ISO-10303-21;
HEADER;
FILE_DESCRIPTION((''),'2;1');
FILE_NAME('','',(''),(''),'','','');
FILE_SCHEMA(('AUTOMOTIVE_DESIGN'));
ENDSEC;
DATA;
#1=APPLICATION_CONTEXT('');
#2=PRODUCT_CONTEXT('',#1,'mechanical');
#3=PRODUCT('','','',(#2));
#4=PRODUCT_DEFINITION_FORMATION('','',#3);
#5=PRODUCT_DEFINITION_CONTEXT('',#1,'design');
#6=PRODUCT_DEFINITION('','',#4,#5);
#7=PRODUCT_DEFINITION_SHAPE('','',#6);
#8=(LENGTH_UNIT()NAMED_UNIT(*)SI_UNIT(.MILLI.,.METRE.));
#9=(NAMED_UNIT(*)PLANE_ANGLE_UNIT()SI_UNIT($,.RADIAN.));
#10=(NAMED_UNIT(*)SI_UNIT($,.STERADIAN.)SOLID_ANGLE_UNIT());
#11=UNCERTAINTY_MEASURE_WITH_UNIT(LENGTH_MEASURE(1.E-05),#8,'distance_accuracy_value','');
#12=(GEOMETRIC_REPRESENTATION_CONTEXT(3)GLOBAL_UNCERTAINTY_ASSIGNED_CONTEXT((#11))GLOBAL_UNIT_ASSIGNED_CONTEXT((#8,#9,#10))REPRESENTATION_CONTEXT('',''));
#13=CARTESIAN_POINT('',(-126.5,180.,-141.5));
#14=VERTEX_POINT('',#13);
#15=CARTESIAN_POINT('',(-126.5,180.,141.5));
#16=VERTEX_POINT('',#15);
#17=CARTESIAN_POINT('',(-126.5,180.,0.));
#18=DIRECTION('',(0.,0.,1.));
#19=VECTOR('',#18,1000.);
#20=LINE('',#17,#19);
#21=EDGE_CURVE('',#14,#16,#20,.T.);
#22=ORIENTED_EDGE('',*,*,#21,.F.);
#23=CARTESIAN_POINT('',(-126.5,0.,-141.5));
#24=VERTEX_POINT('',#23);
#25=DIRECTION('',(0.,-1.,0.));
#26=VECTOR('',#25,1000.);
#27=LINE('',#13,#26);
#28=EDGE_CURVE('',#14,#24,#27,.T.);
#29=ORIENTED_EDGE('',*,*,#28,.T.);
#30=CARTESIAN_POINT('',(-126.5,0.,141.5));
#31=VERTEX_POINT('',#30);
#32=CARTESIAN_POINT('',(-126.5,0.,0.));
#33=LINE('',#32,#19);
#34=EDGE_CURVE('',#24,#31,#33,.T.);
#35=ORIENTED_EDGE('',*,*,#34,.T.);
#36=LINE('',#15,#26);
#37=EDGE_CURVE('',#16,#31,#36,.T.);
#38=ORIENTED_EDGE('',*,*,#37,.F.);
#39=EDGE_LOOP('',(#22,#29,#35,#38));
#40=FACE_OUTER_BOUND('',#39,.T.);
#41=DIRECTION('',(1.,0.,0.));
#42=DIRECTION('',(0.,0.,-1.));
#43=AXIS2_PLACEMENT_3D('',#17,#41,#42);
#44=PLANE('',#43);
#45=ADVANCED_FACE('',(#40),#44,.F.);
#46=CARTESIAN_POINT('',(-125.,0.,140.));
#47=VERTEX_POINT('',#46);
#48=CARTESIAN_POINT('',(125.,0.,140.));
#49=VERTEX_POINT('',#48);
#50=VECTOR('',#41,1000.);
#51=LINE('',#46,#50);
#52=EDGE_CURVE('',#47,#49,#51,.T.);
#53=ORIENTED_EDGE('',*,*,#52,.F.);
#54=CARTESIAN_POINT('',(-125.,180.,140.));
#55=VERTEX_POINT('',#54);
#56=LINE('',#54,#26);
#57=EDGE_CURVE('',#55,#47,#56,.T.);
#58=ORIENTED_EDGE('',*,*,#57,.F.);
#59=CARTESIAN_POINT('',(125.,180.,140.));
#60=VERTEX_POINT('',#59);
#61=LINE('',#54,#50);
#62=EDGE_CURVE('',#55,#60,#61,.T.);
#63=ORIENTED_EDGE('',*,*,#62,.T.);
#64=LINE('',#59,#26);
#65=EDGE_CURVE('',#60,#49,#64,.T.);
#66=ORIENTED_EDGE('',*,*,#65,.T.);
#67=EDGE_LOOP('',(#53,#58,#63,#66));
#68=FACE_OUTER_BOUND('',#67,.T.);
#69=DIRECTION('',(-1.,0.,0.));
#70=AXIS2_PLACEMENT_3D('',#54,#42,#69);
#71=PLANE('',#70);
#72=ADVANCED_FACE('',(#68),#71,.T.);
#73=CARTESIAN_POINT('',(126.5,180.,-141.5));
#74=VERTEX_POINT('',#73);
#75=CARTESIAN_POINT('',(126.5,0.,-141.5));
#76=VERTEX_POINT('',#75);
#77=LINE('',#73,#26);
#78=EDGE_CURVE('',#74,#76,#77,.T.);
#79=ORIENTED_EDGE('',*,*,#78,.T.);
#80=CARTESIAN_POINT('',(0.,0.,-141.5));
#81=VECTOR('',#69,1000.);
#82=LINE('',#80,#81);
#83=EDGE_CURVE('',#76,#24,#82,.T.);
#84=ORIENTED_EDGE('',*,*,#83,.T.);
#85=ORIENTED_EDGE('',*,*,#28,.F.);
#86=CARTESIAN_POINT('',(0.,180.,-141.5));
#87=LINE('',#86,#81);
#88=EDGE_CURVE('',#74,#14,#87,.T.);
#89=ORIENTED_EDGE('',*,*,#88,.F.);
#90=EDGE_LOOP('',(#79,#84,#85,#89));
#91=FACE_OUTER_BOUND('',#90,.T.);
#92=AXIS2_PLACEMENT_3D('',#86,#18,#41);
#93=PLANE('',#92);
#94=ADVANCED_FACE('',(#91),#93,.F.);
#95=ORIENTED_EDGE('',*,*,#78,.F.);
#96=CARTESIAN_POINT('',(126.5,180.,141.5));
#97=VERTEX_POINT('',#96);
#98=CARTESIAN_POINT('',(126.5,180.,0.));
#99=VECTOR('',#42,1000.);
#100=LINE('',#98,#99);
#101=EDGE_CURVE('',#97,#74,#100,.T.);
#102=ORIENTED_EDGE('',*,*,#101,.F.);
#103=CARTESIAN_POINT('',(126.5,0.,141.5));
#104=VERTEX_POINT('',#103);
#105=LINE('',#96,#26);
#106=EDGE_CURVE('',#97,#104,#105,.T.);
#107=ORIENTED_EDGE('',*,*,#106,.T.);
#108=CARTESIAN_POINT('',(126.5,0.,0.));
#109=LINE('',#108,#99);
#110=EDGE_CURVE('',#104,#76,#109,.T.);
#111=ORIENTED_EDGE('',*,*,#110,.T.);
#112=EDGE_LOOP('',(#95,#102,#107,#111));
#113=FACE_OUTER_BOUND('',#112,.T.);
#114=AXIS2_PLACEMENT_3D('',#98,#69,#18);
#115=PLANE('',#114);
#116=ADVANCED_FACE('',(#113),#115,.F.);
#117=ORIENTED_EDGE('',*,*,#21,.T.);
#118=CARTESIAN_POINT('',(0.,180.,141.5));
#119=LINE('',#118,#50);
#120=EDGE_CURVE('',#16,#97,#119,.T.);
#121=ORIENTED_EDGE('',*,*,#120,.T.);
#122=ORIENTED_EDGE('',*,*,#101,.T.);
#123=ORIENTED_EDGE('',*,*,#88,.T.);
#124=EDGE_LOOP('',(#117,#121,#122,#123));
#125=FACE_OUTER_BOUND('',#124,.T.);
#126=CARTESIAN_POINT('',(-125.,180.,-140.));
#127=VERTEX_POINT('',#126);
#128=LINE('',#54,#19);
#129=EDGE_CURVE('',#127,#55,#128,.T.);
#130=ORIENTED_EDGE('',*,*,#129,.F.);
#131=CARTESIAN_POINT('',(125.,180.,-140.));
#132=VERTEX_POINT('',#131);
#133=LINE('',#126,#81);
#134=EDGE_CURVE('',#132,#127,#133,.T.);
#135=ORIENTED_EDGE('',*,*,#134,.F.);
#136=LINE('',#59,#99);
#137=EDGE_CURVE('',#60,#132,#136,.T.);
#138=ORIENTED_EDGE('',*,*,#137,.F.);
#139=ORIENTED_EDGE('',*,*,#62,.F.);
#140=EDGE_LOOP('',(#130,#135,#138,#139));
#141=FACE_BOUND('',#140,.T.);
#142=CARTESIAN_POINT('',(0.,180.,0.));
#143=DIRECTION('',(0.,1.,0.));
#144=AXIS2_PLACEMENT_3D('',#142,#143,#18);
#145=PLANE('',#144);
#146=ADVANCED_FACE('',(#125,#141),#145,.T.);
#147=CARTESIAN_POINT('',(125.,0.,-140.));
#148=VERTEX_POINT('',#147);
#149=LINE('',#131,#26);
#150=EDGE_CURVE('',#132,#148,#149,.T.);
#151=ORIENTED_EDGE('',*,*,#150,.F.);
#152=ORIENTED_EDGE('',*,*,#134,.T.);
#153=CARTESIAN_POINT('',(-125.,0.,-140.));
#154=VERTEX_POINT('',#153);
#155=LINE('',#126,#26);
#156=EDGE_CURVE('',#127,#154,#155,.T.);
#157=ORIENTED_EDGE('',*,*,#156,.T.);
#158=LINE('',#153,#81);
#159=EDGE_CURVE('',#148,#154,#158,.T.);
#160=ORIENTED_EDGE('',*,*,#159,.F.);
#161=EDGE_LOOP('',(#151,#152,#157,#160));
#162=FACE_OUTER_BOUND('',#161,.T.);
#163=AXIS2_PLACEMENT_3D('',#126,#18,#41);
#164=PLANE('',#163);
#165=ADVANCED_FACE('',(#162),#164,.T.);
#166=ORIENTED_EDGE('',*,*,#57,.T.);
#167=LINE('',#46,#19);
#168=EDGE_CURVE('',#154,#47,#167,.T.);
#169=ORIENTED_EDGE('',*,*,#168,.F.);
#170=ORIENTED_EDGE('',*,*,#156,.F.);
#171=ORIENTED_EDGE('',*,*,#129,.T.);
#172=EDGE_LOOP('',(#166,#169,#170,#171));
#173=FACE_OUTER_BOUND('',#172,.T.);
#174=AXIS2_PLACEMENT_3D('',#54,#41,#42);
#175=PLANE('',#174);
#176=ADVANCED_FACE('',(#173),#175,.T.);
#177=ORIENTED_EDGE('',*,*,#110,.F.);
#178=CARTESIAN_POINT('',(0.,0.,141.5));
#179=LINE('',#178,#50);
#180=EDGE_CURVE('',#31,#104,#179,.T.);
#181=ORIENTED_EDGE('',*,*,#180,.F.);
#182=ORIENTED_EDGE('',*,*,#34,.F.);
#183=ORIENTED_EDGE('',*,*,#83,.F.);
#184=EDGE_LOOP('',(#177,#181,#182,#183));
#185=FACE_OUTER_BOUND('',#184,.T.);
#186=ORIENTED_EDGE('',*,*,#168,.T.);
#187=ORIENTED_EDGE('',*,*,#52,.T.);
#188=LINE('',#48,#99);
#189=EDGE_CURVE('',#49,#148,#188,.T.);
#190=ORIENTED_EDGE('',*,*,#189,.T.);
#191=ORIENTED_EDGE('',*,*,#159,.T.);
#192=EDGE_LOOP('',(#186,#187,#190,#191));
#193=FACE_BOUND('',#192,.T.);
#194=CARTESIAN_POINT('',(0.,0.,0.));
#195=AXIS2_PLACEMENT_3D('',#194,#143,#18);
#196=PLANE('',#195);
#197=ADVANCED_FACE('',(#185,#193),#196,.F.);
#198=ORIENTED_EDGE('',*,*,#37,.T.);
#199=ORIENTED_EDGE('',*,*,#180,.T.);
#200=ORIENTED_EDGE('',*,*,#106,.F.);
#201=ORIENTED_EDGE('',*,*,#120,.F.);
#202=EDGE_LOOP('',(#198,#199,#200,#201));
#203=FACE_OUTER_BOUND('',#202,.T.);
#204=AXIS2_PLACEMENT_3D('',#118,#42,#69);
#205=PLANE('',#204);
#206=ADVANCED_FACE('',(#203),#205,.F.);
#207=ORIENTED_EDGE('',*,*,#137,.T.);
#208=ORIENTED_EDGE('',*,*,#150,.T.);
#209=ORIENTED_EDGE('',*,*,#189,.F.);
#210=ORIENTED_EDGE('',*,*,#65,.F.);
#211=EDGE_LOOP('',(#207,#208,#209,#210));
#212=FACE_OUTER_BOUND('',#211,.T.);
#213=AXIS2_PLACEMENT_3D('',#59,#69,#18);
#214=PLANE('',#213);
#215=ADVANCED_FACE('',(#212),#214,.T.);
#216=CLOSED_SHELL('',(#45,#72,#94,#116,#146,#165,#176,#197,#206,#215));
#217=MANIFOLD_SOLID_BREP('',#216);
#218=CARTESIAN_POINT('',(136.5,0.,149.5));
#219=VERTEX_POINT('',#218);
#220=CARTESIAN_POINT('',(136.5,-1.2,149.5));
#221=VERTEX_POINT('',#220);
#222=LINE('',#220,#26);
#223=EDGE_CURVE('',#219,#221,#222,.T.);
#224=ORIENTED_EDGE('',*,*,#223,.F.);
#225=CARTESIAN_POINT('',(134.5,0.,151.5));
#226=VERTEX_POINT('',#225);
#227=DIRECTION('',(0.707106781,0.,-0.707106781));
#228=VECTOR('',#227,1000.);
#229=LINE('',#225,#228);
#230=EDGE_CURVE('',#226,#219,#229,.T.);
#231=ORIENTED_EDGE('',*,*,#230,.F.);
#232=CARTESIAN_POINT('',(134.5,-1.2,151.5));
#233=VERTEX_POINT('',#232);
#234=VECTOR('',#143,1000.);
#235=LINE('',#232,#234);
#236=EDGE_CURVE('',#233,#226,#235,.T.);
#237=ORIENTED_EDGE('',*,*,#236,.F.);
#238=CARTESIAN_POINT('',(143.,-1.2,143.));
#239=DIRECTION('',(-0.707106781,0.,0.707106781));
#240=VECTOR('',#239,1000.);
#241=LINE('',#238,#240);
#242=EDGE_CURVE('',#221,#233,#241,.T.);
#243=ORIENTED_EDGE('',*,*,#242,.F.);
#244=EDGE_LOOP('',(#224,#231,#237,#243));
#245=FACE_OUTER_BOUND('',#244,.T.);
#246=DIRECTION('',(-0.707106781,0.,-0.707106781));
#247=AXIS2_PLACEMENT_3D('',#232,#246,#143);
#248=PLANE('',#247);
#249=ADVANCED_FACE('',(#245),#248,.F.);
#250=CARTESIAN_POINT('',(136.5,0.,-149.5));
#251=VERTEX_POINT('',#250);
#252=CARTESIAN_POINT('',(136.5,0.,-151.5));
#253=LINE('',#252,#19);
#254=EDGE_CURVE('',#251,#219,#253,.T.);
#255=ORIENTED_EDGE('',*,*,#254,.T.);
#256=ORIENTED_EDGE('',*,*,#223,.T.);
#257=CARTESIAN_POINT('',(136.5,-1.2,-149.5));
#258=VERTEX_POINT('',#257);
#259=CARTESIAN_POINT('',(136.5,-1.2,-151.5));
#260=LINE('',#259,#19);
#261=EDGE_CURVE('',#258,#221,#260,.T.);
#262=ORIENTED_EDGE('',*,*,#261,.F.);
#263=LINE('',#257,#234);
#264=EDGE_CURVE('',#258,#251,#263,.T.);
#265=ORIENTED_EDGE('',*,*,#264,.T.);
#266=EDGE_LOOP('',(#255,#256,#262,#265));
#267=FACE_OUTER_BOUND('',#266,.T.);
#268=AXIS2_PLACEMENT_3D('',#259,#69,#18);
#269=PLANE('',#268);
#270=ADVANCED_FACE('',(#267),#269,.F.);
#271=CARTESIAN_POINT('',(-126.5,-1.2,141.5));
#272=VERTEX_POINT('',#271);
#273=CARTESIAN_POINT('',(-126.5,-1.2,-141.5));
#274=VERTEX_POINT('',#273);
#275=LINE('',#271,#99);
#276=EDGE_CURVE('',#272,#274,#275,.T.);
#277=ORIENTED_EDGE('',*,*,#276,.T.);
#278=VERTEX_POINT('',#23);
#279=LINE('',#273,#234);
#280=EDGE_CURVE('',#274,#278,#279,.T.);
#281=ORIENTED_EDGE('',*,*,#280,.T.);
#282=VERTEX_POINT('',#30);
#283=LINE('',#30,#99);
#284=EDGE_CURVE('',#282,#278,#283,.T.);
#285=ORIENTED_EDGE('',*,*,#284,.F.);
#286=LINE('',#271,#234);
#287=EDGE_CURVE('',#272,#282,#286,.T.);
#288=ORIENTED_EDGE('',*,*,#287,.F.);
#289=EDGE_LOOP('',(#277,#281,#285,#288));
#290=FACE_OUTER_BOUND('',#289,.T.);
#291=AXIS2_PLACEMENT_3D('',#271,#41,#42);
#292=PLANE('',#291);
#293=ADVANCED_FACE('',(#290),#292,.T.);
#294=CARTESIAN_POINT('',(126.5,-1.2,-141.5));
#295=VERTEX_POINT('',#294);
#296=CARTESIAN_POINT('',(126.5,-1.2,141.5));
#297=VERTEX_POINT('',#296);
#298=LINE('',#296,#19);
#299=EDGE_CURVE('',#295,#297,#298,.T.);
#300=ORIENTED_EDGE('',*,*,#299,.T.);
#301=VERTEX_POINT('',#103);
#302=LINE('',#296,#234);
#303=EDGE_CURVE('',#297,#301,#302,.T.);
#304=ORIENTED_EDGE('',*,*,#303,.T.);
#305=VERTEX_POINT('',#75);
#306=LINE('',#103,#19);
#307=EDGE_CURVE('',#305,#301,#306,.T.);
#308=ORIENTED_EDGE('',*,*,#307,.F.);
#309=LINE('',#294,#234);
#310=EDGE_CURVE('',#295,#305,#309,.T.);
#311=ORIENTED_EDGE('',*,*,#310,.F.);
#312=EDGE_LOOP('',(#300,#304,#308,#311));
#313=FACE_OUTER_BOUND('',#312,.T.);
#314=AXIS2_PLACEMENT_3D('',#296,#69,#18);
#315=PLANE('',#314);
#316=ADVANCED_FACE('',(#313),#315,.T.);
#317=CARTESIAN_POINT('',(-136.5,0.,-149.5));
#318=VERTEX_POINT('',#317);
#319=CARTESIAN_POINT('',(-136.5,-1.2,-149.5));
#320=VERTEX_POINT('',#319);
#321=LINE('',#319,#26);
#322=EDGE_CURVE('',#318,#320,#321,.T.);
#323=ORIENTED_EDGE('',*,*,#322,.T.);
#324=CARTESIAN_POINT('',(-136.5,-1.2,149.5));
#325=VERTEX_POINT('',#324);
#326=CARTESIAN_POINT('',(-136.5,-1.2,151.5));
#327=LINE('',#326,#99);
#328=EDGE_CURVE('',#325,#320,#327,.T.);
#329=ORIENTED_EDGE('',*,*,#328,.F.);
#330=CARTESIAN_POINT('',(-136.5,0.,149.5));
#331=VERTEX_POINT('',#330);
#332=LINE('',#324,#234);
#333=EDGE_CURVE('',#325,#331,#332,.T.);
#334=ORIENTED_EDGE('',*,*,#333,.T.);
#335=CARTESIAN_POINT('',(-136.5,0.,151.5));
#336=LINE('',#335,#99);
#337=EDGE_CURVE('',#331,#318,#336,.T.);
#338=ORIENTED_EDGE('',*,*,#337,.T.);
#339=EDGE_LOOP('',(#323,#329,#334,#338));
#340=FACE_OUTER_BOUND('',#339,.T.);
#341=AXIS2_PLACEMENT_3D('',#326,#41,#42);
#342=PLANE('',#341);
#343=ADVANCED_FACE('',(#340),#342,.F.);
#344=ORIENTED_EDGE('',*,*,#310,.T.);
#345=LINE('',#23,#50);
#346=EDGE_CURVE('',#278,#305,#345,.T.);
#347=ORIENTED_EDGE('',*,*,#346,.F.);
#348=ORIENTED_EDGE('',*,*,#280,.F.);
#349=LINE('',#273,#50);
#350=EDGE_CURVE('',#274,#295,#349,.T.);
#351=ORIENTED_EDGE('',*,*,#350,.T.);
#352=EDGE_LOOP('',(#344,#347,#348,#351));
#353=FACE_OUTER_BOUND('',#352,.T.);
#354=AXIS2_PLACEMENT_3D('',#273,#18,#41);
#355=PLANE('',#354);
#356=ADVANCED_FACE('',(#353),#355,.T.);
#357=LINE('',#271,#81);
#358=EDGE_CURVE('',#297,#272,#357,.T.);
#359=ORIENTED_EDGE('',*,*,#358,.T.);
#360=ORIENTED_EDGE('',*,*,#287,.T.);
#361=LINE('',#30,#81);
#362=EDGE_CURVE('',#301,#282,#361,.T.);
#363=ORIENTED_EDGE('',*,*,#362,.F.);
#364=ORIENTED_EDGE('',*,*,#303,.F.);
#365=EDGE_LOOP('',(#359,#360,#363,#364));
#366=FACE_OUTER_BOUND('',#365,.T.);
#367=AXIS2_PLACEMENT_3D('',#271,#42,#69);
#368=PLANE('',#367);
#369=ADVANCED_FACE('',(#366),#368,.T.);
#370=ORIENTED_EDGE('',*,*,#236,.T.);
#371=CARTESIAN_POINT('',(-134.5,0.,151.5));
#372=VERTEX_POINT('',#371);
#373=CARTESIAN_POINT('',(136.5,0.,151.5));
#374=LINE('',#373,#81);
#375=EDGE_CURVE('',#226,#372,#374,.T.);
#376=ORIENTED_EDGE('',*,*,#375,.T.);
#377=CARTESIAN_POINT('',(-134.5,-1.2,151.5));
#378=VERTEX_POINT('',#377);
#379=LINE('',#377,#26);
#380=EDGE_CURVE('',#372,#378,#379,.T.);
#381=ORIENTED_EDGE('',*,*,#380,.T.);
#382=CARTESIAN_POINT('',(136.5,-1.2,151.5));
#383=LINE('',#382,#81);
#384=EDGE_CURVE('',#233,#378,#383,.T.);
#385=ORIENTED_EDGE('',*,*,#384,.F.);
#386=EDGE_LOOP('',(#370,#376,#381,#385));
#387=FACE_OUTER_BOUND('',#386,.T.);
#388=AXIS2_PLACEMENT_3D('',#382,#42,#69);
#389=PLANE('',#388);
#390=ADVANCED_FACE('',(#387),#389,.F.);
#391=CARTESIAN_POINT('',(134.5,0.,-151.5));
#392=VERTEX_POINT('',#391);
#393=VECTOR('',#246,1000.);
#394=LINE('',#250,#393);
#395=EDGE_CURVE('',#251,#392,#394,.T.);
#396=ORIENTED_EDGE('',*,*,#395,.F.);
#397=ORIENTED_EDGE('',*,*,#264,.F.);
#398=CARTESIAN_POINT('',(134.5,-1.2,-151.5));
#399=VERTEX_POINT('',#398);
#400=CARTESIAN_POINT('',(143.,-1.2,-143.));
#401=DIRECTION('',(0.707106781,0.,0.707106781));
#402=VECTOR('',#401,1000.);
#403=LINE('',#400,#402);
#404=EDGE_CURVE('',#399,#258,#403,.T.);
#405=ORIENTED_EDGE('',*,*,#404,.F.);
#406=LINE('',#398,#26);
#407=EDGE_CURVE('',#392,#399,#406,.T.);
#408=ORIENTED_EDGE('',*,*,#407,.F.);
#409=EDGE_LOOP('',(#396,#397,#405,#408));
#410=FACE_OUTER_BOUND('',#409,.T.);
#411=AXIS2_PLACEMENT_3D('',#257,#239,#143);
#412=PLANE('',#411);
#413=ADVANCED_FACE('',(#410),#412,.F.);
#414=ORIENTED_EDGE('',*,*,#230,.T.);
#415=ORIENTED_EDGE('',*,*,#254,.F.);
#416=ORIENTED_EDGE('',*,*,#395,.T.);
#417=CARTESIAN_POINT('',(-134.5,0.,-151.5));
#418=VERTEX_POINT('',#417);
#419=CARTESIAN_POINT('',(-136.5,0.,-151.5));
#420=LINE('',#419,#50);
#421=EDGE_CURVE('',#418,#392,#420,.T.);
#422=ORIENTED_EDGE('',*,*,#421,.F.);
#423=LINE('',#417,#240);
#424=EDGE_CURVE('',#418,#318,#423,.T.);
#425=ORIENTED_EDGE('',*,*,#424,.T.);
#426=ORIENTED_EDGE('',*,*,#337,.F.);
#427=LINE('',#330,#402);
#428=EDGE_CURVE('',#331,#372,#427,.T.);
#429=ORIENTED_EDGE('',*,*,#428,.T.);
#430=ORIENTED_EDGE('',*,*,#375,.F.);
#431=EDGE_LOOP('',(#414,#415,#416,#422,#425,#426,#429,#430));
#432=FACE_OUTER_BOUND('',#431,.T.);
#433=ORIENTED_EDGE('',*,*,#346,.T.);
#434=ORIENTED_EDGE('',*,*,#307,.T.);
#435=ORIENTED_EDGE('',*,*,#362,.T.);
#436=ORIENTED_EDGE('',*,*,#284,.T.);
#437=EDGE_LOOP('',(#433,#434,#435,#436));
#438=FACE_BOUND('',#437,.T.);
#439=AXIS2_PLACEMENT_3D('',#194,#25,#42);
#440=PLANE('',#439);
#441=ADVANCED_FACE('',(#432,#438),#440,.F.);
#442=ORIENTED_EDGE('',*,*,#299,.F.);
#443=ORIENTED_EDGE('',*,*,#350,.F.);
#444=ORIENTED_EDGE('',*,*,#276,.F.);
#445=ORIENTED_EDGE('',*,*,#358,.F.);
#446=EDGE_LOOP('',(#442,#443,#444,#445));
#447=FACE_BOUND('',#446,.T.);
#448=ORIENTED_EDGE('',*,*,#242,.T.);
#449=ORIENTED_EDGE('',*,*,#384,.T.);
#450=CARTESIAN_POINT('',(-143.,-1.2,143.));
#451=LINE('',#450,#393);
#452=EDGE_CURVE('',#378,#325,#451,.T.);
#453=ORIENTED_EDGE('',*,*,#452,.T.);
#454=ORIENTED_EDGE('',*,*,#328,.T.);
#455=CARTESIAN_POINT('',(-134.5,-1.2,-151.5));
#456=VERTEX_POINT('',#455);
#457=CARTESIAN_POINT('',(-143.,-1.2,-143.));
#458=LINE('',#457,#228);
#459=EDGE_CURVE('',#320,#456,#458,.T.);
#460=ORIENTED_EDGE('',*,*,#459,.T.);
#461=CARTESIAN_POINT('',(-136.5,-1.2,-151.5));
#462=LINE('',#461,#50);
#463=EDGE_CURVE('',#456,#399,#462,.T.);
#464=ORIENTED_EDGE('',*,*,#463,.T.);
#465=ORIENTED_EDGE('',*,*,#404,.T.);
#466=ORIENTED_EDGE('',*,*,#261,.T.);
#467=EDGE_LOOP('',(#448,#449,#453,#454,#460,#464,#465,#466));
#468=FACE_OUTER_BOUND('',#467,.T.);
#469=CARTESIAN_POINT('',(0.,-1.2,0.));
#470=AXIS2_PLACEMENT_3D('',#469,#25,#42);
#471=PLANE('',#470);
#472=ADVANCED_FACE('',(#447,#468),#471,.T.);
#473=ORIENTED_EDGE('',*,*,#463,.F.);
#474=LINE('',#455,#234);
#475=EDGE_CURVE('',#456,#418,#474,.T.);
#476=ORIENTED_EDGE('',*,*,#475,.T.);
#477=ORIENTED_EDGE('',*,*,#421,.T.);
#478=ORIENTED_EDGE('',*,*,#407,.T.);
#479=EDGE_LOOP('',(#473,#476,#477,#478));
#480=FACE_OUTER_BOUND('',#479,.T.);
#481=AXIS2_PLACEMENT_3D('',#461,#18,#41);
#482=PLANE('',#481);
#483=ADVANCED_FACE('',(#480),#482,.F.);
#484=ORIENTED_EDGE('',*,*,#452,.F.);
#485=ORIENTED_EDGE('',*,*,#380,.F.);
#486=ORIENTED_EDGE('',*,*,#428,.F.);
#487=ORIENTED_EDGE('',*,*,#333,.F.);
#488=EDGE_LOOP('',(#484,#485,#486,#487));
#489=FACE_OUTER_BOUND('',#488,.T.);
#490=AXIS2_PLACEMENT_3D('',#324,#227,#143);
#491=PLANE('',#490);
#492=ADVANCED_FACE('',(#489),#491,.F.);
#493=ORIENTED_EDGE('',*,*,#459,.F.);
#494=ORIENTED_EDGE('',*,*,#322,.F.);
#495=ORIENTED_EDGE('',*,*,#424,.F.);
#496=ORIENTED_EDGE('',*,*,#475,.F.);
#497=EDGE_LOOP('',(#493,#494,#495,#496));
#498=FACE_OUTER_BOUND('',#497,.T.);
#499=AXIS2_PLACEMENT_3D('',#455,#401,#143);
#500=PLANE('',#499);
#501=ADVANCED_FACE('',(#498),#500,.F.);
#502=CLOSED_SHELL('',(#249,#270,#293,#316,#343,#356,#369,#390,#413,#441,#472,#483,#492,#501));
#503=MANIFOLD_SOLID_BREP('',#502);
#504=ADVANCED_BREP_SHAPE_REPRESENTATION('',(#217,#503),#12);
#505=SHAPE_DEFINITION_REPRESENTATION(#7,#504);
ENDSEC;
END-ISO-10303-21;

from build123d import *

# Parameters (mm, degrees)
SKETCH_1_W        = 253
SKETCH_1_H        = 283
SKETCH_1_W_2      = 250
SKETCH_1_H_2      = 280
EXTRUDE_1_DEPTH   = 180
SKETCH_2_W        = 273
SKETCH_2_H        = 303
SKETCH_2_W_2      = 253
SKETCH_2_H_2      = 283
EXTRUDE_1_2_DEPTH = 1.2
CHAMFER_1_SIZE    = 2


with BuildPart() as part:
    # 草图1 → Extrude 1 (new body)
    with BuildSketch(Plane(origin=(0, 0, 0), x_dir=(1, 0, 0), z_dir=(0, 1, 0))):
        Rectangle(SKETCH_1_W, SKETCH_1_H)
        Rectangle(SKETCH_1_W_2, SKETCH_1_H_2, mode=Mode.SUBTRACT)
    extrude(amount=EXTRUDE_1_DEPTH)


with BuildPart() as body_2:
    # 草图2 → Extrude 1 2 (new body)
    with BuildSketch(Plane.XZ):
        Rectangle(SKETCH_2_W, SKETCH_2_H)
        Rectangle(SKETCH_2_W_2, SKETCH_2_H_2, mode=Mode.SUBTRACT)
    extrude(amount=EXTRUDE_1_2_DEPTH)

    # 倒角1
    chamfer_1_edges = [body_2.edges().sort_by_distance(p)[0] for p in [
        (-136.5, -0.6, -151.5),
        (-136.5, -0.6, 151.5),
        (136.5, -0.6, 151.5),
        (136.5, -0.6, -151.5),
    ]]
    chamfer(chamfer_1_edges, length=CHAMFER_1_SIZE)


solid = Compound([part.part, body_2.part])
